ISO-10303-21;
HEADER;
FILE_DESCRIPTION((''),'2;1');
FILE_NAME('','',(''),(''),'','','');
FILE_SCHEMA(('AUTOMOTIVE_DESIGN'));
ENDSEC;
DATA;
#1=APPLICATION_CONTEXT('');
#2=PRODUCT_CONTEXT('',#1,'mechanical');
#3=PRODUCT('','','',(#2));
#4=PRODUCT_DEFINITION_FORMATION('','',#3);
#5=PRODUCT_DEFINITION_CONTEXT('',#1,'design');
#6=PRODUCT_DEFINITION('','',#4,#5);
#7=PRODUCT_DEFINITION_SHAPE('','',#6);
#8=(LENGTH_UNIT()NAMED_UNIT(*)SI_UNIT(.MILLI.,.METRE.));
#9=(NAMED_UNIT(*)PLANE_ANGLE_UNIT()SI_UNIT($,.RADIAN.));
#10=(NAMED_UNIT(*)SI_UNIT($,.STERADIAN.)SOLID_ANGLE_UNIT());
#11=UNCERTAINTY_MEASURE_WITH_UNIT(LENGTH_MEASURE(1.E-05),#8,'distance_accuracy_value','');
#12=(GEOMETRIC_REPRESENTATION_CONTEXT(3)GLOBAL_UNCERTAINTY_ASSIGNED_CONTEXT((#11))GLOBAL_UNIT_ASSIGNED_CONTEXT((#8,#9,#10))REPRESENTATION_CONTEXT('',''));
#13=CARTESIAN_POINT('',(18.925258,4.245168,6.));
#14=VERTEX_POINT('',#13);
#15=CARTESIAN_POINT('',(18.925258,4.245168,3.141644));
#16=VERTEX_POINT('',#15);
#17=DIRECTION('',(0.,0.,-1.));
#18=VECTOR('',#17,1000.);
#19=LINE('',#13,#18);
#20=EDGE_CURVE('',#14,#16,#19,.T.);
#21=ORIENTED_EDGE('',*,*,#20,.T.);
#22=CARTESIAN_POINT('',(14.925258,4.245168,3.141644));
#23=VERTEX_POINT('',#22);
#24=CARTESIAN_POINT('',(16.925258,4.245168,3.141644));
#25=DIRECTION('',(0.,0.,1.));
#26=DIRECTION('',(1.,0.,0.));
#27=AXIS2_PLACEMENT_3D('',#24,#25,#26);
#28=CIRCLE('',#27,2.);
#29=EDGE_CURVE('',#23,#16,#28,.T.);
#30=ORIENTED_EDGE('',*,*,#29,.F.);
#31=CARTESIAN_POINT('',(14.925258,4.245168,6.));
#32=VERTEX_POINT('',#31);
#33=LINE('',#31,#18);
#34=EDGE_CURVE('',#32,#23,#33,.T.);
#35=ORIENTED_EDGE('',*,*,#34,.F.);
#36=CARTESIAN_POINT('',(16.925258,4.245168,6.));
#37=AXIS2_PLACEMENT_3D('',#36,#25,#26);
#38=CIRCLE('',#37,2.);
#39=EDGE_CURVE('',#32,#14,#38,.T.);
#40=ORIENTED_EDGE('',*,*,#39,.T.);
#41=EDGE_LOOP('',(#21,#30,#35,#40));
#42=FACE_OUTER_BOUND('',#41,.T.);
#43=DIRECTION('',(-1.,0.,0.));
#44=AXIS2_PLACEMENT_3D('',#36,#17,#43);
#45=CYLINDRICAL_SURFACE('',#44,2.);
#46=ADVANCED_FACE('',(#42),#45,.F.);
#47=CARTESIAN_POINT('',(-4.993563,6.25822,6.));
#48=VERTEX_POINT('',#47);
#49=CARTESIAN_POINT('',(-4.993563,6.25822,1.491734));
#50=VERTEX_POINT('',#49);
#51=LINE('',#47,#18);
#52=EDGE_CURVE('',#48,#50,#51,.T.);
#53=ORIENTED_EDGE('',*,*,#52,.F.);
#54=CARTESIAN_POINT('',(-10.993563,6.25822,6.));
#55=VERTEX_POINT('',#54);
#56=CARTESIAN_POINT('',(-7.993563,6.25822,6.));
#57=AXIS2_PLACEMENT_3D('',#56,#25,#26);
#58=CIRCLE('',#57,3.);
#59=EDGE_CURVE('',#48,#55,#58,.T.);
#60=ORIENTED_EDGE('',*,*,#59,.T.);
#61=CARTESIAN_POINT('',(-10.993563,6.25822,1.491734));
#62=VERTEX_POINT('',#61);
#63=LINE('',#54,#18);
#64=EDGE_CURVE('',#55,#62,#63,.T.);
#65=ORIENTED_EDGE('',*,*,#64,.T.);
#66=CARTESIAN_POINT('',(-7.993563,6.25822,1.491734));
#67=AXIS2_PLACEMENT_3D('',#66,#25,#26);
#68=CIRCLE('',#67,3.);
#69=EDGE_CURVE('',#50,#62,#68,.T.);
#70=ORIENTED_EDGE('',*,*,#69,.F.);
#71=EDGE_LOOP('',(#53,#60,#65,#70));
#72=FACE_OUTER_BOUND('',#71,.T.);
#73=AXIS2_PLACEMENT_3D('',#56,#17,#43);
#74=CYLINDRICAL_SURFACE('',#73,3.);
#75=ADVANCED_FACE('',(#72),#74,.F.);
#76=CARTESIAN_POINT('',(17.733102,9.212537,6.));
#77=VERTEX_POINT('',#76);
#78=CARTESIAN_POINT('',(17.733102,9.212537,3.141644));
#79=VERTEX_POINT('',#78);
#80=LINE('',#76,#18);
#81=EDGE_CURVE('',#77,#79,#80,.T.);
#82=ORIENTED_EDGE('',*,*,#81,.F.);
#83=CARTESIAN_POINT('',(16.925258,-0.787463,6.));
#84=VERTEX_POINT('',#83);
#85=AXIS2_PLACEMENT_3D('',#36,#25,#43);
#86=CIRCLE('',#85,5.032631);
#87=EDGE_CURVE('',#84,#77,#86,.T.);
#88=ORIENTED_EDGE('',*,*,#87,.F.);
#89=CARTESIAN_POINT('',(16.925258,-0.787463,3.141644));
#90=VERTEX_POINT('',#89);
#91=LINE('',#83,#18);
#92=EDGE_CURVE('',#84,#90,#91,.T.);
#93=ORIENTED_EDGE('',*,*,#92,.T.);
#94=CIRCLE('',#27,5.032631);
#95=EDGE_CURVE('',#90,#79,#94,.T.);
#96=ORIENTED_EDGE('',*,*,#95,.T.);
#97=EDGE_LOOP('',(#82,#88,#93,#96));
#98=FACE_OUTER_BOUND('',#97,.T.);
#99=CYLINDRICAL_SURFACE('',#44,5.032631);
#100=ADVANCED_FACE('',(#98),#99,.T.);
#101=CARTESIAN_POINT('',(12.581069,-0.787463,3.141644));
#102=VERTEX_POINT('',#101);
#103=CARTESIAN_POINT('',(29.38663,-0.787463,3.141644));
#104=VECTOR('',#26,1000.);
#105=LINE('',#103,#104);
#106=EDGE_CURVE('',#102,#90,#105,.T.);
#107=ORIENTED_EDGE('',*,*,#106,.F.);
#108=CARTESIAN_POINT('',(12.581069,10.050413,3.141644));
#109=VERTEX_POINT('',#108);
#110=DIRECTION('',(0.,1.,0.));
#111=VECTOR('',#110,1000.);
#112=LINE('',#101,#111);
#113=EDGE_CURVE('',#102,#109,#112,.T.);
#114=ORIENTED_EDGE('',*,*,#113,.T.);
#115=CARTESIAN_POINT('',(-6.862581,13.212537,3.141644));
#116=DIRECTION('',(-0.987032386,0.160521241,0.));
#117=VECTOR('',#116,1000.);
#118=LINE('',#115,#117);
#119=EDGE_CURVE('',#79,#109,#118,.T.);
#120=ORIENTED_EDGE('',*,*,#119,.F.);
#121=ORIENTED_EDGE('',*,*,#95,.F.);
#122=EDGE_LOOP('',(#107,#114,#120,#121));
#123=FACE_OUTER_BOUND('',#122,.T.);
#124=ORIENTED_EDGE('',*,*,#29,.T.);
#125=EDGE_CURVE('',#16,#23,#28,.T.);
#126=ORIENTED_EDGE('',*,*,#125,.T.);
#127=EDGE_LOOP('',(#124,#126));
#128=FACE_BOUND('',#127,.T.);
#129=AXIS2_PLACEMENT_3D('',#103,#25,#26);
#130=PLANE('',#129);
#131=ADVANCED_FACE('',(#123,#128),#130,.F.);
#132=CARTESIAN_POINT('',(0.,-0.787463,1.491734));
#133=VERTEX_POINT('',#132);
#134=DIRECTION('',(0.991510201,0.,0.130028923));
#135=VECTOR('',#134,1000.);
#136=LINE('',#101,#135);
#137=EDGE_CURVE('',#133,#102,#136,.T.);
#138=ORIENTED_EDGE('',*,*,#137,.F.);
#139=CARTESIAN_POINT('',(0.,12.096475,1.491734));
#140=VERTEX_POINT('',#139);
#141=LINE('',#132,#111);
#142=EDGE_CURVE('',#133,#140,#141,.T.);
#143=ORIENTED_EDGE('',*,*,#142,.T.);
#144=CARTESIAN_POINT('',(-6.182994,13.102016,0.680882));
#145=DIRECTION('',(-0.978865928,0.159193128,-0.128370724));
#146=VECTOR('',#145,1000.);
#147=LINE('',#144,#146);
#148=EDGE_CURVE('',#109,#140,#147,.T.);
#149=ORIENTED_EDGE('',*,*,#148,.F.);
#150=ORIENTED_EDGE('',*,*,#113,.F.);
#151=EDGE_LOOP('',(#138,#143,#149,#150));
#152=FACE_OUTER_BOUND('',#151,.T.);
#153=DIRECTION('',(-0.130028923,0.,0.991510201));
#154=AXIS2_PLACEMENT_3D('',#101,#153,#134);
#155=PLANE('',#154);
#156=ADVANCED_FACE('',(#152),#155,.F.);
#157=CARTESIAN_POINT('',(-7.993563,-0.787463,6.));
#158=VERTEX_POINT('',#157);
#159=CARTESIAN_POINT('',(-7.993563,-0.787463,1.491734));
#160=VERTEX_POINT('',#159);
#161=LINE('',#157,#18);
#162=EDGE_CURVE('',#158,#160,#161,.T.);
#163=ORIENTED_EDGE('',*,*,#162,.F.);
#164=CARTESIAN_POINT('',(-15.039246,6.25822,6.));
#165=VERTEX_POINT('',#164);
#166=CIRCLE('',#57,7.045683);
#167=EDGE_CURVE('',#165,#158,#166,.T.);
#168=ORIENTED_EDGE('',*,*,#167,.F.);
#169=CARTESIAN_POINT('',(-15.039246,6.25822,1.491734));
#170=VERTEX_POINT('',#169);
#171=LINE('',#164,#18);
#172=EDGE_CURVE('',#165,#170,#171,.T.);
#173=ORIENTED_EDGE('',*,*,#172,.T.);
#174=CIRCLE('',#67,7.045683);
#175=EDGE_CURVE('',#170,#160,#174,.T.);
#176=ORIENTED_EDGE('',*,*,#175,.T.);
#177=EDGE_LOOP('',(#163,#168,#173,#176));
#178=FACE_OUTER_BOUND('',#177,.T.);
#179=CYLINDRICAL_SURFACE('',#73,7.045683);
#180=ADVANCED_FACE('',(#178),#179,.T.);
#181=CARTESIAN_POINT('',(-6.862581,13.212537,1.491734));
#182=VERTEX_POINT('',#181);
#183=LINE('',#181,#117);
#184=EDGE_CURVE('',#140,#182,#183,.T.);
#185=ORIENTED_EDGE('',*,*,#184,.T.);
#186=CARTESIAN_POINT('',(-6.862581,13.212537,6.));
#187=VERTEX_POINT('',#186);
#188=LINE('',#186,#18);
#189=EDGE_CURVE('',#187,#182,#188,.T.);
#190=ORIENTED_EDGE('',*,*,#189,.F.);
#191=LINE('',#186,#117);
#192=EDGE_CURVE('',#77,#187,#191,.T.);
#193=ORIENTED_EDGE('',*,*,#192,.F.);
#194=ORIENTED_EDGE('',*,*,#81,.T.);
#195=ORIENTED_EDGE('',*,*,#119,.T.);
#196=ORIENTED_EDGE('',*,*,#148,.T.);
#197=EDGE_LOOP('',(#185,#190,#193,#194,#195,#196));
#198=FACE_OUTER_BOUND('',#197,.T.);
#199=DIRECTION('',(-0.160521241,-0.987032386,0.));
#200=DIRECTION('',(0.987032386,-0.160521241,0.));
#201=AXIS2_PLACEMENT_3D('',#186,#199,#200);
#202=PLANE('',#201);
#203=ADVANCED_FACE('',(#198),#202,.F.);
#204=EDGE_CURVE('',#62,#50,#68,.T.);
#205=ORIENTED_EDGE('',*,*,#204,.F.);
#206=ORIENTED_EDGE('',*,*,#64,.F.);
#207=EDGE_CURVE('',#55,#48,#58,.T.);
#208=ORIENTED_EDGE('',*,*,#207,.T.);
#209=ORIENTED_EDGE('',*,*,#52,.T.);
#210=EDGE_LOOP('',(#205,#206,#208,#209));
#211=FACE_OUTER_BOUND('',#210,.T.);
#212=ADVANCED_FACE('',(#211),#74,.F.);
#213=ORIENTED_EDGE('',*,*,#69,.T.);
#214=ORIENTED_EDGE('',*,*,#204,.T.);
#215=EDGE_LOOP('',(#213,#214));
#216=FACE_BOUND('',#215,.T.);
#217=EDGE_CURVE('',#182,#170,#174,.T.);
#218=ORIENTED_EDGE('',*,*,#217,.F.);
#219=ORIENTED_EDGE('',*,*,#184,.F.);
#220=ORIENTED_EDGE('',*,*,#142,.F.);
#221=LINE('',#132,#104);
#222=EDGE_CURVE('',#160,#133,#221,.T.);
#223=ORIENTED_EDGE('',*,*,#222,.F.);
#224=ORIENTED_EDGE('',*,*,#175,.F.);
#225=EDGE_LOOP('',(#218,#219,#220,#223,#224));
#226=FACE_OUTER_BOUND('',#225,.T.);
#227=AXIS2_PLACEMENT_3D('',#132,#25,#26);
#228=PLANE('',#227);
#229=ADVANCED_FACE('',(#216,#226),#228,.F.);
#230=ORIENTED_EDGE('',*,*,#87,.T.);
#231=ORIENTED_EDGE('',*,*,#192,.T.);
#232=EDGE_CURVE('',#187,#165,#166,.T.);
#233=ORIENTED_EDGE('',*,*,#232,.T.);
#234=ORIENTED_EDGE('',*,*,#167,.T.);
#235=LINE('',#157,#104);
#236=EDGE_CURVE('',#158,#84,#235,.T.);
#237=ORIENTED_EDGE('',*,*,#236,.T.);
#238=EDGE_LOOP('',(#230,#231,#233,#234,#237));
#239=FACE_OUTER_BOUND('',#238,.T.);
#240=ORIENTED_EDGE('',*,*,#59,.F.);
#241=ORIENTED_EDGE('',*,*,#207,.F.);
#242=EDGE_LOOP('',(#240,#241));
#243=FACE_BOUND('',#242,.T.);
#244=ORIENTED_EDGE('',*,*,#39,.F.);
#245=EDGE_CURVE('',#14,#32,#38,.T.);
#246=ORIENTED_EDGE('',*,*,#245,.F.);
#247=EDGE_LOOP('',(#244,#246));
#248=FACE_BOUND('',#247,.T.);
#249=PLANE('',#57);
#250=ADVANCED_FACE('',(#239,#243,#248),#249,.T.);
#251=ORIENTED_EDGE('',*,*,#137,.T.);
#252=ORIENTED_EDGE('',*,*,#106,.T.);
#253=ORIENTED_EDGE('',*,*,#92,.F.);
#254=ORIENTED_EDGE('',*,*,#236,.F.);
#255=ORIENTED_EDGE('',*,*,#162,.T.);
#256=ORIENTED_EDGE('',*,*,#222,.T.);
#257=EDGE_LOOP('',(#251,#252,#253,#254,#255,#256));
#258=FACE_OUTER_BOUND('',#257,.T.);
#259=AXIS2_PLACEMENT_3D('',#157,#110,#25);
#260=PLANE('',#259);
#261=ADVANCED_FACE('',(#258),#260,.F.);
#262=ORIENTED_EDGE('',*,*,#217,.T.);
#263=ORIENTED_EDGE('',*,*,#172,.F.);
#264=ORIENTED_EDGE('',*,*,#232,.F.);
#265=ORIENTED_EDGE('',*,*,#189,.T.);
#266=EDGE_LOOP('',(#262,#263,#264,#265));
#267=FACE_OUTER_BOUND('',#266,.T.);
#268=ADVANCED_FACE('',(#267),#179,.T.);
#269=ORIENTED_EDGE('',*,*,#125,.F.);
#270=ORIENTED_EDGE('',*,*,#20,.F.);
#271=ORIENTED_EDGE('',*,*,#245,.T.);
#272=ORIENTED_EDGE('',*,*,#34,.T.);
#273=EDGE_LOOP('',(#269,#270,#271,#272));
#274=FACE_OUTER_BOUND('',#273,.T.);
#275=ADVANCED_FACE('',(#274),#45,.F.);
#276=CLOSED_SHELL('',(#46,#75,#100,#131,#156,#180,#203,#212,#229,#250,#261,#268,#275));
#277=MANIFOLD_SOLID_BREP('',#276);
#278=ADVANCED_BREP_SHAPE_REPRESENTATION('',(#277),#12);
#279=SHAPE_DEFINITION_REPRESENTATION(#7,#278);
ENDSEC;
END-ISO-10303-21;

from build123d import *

# Parameters (mm, degrees)
SKETCH1_R               = 2
SKETCH1_R_2             = 3
BOSS_EXTRUDE1_DEPTH     = 6
CUT_EXTRUDE1_DEPTH      = 27.36555884
CUT_EXTRUDE1_DEPTH_BACK = 27.36555884


with BuildPart() as part:
    # Sketch1 → Boss-Extrude1 (new body)
    with BuildSketch(Plane.XY):
        with BuildLine():
            Line((-7.993562913, -0.787462727), (16.925257698, -0.787462727))
            ThreePointArc((16.925257698, -0.787462727), (21.941546469, 3.839929946), (17.733101807, 9.212537273))
            Line((17.733101807, 9.212537273), (-6.862581161, 13.212537273))
            ThreePointArc((-6.862581161, 13.212537273), (-15.016367191, 6.825553227), (-7.993562913, -0.787462727))
        make_face()
        with Locations((16.925257698, 4.245167879)):
            Circle(SKETCH1_R, mode=Mode.SUBTRACT)
        with Locations((-7.993562913, 6.258220121)):
            Circle(SKETCH1_R_2, mode=Mode.SUBTRACT)
    extrude(amount=BOSS_EXTRUDE1_DEPTH)

    # Sketch2 → Cut-Extrude1 (cut, two sides: drawn at the far end of the back side and taken through both)
    with BuildSketch(Plane(origin=(0, 0, 0), x_dir=(1, 0, 0), z_dir=(0, 1, 0)).offset(-CUT_EXTRUDE1_DEPTH_BACK)):
        Polygon((29.386629895, -3.141643917), (12.58106894, -3.141643917), (0, -1.491733663), (-17.019149761, -1.491733663), (-15.478750308, 10.25428202), (32.017830731, 8.260226372), align=None)
    extrude(amount=CUT_EXTRUDE1_DEPTH + CUT_EXTRUDE1_DEPTH_BACK, mode=Mode.SUBTRACT)


solid = part.part
